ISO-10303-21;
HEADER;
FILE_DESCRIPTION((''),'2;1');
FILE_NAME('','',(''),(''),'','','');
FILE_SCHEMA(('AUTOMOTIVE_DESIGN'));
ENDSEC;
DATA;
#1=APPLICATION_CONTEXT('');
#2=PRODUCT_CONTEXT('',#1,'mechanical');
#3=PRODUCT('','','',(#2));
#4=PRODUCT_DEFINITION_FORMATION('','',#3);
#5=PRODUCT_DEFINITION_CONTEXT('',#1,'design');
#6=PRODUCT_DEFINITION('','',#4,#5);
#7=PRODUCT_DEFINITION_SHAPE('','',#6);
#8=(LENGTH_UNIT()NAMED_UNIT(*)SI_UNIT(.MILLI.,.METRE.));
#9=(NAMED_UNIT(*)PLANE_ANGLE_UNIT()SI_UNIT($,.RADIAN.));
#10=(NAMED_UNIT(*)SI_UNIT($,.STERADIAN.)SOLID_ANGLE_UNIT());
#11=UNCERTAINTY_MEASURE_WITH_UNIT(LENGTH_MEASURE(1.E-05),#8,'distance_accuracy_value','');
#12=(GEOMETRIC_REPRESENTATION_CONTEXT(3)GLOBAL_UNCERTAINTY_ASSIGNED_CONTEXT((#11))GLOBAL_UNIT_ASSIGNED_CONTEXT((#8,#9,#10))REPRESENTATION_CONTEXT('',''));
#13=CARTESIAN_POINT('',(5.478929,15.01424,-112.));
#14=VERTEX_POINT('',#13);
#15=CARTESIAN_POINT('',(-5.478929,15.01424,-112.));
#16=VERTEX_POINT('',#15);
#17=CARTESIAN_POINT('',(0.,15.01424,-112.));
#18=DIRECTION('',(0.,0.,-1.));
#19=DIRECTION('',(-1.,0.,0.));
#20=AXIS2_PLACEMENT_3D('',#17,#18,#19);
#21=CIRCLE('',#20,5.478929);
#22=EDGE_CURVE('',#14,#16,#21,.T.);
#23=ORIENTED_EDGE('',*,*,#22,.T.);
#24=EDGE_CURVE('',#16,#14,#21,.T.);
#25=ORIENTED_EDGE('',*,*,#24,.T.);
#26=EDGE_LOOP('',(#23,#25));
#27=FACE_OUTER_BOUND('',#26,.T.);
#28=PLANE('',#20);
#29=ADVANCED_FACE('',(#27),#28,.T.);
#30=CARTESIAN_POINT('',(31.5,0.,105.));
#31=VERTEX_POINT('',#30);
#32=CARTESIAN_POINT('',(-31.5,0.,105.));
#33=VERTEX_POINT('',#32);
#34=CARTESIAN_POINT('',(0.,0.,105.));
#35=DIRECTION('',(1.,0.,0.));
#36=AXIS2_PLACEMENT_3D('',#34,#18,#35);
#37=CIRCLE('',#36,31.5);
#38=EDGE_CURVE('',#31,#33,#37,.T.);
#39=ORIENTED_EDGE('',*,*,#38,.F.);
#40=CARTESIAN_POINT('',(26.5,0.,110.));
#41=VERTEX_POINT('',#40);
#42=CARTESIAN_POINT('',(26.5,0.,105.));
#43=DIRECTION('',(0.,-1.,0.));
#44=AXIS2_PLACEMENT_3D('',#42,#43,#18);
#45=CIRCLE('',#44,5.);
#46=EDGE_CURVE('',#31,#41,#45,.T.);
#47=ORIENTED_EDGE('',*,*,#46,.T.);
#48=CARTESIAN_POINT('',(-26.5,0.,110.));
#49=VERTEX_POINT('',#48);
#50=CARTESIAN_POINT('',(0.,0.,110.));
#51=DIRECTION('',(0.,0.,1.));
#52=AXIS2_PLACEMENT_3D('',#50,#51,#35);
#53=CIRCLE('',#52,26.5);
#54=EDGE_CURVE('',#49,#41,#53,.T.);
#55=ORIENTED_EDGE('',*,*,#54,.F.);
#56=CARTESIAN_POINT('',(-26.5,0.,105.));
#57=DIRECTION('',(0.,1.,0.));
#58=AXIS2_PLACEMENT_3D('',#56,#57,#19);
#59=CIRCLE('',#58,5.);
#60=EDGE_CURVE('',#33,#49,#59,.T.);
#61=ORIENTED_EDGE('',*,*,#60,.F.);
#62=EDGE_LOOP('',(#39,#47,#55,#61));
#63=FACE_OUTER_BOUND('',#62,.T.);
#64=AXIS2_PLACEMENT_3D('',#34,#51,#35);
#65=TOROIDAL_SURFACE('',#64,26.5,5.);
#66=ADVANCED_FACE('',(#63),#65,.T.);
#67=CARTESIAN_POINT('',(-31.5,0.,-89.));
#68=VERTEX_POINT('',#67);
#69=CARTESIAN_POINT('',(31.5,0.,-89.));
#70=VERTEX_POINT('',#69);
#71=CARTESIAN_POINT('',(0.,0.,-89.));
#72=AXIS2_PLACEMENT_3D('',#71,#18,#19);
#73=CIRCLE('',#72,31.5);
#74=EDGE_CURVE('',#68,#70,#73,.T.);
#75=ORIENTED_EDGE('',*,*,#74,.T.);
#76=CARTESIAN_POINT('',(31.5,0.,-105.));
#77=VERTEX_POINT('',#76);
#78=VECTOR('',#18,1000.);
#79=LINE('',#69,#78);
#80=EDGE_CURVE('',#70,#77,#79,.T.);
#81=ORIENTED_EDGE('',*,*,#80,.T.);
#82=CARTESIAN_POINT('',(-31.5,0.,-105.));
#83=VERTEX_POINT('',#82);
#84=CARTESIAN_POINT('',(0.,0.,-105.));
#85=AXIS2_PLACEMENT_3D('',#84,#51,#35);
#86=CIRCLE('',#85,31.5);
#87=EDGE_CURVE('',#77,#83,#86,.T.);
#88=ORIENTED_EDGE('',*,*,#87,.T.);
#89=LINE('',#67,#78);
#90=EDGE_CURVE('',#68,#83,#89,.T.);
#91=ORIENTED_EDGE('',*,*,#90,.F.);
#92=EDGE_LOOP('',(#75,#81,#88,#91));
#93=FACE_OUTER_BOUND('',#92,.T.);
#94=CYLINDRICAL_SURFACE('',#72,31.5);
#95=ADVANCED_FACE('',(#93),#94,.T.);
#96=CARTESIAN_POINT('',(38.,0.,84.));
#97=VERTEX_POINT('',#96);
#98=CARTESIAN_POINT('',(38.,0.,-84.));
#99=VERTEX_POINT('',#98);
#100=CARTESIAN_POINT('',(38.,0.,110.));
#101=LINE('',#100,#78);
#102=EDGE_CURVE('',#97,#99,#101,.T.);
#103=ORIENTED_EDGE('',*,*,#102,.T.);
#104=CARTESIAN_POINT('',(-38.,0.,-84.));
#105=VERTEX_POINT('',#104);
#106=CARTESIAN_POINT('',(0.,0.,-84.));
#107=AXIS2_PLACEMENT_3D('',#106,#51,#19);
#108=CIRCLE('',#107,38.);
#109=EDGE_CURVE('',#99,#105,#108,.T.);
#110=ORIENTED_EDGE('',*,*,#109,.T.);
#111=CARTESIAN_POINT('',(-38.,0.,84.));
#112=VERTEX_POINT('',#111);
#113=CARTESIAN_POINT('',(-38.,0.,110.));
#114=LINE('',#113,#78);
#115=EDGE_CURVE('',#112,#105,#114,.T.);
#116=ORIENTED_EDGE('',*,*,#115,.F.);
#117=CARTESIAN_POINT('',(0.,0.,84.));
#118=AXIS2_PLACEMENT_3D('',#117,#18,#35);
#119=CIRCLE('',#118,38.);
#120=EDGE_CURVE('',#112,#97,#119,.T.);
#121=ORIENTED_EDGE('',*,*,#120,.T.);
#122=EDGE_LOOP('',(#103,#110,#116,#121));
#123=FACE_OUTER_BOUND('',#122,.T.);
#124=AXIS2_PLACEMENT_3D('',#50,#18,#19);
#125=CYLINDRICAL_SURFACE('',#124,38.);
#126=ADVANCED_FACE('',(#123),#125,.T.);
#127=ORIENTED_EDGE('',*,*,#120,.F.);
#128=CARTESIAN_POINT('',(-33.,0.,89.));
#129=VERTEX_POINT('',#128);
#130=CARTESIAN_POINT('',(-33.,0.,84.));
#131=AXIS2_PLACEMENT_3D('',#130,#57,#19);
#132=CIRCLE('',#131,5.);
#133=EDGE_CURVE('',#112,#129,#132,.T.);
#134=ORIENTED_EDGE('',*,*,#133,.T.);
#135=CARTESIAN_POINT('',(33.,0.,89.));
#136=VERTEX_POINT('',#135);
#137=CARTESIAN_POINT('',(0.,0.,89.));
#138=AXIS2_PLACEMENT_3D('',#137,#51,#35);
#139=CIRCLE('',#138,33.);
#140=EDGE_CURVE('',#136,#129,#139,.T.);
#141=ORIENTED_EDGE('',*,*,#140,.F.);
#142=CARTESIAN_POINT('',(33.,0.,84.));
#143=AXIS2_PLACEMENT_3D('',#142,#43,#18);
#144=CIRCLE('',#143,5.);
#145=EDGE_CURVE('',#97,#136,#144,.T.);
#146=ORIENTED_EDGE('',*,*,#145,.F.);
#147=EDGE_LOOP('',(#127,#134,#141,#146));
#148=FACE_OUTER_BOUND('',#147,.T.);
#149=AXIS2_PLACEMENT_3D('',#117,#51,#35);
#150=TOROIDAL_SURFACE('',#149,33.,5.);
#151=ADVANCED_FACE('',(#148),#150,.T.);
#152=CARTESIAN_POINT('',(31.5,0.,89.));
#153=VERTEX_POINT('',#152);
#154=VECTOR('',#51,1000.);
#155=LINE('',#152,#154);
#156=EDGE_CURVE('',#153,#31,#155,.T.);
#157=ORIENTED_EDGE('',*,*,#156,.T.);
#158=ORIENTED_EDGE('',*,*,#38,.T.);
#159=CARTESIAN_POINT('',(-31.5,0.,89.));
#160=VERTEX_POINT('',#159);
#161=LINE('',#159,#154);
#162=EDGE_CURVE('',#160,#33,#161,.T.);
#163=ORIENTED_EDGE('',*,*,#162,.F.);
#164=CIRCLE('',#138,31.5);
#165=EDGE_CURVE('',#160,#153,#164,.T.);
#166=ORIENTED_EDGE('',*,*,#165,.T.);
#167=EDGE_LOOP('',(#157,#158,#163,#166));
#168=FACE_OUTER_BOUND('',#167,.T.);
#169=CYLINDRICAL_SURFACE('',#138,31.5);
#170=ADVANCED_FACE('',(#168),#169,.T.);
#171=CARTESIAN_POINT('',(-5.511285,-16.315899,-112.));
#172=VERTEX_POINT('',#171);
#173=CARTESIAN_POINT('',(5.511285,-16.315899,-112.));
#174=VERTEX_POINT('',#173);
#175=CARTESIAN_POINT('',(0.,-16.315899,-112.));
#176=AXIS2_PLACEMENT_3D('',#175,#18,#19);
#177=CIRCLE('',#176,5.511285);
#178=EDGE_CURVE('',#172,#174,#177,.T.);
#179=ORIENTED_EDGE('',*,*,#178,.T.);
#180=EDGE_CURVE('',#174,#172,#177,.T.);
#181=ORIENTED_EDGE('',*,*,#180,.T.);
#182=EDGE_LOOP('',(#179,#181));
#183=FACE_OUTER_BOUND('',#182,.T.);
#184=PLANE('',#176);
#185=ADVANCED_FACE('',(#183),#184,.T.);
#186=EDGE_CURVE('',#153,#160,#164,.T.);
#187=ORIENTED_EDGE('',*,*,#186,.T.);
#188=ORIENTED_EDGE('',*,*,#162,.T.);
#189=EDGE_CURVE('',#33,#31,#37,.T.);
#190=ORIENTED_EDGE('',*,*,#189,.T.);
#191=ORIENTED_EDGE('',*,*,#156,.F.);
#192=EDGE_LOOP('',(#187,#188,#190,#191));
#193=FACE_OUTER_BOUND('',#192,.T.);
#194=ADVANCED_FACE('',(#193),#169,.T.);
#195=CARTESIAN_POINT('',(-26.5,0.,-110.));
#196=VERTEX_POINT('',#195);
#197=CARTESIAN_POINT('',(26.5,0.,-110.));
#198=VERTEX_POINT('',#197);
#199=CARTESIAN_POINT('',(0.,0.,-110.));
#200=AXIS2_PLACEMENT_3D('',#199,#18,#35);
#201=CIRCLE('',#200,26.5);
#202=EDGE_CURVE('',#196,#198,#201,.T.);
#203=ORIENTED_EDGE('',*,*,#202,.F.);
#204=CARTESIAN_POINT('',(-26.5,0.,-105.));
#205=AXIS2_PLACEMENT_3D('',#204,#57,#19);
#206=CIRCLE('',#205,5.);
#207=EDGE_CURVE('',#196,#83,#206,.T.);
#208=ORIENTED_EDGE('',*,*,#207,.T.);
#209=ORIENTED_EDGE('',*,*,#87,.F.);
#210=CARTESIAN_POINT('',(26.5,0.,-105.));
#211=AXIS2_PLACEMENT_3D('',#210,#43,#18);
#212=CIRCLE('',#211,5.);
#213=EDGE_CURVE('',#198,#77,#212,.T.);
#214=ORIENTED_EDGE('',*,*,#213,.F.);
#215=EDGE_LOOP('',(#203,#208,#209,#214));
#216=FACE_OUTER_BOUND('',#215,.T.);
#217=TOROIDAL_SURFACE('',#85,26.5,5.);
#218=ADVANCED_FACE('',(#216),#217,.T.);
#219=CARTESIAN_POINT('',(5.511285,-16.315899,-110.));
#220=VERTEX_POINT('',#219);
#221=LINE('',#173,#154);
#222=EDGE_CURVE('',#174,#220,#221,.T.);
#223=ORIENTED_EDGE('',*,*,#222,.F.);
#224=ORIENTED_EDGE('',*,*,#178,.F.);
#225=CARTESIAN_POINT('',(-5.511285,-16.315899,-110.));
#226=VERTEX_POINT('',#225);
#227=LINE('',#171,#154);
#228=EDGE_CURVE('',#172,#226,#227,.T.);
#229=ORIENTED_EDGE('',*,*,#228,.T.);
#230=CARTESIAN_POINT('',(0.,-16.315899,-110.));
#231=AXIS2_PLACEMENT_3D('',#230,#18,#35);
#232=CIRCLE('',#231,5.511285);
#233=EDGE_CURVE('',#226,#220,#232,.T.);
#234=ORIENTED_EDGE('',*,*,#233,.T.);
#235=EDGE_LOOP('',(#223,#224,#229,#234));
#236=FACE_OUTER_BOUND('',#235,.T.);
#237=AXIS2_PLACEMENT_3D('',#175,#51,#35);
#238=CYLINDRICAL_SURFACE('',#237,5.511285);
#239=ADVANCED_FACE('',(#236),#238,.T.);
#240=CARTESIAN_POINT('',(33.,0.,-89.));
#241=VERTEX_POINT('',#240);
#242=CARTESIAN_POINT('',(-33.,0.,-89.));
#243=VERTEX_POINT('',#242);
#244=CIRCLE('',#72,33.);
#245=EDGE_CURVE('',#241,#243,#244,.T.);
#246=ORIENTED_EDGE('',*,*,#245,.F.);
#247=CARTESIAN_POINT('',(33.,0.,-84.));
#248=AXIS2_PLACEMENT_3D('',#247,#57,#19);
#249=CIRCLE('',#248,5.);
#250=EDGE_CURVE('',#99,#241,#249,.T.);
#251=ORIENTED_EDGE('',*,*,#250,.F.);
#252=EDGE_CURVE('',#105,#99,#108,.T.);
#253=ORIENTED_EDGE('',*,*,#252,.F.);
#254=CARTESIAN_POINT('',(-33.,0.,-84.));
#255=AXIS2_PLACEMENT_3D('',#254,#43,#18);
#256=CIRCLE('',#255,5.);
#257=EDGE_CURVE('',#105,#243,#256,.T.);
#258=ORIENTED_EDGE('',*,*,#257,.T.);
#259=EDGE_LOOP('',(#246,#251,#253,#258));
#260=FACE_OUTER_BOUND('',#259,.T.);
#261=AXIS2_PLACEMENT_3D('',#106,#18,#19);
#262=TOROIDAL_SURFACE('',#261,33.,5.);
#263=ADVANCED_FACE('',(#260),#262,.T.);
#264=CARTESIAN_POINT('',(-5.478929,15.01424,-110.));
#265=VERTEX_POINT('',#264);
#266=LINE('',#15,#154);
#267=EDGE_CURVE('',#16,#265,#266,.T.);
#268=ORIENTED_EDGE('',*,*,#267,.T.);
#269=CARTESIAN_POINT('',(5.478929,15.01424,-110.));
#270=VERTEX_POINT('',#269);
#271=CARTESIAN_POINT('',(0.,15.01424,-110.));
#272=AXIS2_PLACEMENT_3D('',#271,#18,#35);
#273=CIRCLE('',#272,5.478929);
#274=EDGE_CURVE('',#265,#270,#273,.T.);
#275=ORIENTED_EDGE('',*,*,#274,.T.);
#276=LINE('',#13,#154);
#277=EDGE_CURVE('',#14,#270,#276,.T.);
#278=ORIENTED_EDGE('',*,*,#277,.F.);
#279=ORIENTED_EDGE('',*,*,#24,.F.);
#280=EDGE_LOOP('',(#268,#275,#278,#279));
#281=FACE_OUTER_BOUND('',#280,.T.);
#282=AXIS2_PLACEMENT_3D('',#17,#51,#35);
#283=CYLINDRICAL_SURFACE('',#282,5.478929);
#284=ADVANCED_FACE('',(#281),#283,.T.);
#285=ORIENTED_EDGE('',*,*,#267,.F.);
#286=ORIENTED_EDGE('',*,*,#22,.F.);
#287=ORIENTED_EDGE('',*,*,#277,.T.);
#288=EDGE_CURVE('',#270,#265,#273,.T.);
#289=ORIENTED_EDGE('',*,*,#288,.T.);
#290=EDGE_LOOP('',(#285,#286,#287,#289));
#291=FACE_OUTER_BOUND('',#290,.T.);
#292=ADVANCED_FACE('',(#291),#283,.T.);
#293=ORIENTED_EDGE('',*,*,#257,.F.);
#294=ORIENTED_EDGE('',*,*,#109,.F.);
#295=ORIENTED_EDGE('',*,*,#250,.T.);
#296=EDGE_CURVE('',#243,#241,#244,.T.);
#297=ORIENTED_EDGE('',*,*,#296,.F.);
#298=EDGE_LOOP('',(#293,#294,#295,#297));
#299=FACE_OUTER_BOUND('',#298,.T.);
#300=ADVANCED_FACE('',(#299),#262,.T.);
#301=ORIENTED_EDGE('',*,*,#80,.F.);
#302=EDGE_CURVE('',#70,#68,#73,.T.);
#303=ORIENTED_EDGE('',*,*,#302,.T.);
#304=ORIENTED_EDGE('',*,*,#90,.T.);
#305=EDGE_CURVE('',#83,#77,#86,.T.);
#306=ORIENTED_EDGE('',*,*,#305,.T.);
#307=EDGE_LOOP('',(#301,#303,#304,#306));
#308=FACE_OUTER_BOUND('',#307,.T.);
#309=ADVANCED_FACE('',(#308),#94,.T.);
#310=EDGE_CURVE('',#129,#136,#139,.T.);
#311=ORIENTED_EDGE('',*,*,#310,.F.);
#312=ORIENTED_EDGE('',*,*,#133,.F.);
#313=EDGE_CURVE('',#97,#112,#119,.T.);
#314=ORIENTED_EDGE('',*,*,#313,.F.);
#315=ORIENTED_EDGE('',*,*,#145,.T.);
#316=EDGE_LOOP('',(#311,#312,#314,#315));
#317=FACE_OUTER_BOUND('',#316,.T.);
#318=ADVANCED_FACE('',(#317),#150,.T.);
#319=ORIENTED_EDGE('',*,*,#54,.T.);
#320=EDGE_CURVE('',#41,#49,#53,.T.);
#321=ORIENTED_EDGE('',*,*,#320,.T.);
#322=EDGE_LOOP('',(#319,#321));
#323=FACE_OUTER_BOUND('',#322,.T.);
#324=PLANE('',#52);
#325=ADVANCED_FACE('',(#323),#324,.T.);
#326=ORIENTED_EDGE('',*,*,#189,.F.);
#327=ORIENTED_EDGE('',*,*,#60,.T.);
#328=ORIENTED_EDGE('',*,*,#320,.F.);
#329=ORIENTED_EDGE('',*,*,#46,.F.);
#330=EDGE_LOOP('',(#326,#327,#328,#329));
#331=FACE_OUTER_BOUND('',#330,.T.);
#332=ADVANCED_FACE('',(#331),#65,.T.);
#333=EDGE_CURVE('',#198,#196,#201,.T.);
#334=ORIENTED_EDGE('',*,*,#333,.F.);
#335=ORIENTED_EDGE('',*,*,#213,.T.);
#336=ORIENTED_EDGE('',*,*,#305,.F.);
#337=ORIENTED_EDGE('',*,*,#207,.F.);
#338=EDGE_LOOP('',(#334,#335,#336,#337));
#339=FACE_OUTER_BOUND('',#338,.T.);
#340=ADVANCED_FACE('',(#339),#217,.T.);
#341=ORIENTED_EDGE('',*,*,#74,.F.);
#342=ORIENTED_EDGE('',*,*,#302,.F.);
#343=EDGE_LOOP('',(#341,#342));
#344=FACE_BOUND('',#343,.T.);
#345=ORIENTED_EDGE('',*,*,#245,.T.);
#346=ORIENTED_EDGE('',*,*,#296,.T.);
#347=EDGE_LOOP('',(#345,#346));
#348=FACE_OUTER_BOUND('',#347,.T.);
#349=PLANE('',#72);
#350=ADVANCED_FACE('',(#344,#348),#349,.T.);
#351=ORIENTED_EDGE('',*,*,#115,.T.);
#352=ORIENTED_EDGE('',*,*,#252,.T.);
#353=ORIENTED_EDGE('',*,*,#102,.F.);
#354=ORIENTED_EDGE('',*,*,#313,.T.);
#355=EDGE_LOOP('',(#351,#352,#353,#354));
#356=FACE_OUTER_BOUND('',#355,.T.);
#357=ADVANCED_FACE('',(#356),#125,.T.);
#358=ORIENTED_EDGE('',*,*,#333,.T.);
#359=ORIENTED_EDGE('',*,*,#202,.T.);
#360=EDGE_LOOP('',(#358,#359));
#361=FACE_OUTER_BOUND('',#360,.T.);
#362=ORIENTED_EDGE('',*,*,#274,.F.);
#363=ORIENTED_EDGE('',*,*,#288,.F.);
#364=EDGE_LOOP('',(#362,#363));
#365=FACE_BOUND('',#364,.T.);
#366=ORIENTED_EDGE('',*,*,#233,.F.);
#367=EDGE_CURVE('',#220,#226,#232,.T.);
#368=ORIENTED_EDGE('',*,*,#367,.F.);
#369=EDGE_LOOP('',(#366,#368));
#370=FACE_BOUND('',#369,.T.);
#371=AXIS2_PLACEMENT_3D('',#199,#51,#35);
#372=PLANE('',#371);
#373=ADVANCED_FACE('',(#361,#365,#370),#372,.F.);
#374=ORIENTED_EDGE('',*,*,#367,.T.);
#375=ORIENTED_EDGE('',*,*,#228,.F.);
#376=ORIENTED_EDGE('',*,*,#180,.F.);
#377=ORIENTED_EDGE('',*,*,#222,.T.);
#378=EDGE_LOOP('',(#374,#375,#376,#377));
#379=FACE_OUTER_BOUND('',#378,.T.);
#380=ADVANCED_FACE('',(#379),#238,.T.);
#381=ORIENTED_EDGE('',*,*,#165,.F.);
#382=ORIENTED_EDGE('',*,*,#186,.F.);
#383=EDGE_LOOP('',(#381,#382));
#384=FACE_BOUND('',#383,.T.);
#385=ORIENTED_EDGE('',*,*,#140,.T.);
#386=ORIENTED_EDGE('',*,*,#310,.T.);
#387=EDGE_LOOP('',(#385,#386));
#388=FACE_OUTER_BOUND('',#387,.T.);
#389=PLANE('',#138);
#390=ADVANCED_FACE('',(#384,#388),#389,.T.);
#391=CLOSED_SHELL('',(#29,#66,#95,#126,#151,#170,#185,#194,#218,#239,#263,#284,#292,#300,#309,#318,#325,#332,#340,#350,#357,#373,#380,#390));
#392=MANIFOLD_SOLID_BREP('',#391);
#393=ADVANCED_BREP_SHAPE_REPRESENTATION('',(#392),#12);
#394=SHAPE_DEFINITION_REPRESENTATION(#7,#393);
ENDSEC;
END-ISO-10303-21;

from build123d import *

# Parameters (mm, degrees)
SKETCH_1_R          = 38
EXTRUDE_1_DEPTH     = 110
SKETCH_4_OUTSIDE_W  = 126.97
SKETCH_4_OUTSIDE_H  = 126.97
SKETCH_4_OUTSIDE_R  = 31.5
CUT_EXTRUDE_1_DEPTH = 21
SKETCH_5_OUTSIDE_W  = 126.97
SKETCH_5_OUTSIDE_H  = 126.97
SKETCH_5_OUTSIDE_R  = 31.5
CUT_EXTRUDE_2_DEPTH = 21
FILLET_1_R          = 5
SKETCH_2_R          = 5.478928785
SKETCH_2_R_2        = 5.511284945
EXTRUDE_2_DEPTH     = 2


with BuildPart() as part:
    # 草图1 → 凸台-拉伸1 (new, symmetric)
    with BuildSketch(Plane.XY):
        Circle(SKETCH_1_R)
    extrude(amount=EXTRUDE_1_DEPTH, both=True)

    # 草图4 outside → 切除-拉伸1 (cut)
    with BuildSketch(Plane.XY.offset(110)):
        Rectangle(SKETCH_4_OUTSIDE_W, SKETCH_4_OUTSIDE_H)
        Circle(SKETCH_4_OUTSIDE_R, mode=Mode.SUBTRACT)
    extrude(amount=-CUT_EXTRUDE_1_DEPTH, mode=Mode.SUBTRACT)

    # 草图5 outside → 切除-拉伸2 (cut)
    with BuildSketch(Plane(origin=(0, 0, -110), x_dir=(-1, 0, 0), z_dir=(0, 0, -1))):
        Rectangle(SKETCH_5_OUTSIDE_W, SKETCH_5_OUTSIDE_H)
        with Locations(Location((0, 0, 0), (0, 0, 180))):
            Circle(SKETCH_5_OUTSIDE_R, mode=Mode.SUBTRACT)
    extrude(amount=-CUT_EXTRUDE_2_DEPTH, mode=Mode.SUBTRACT)

    # 圆角1
    fillet_1_edges = [part.edges().sort_by_distance(p)[0] for p in [
        (-31.5, 0, 110),
        (-38, 0, -89),
        (-31.5, 0, -110),
        (-38, 0, 89),
    ]]
    fillet(fillet_1_edges, radius=FILLET_1_R)

    # 草图2 → 凸台-拉伸2 (add)
    with BuildSketch(Plane(origin=(0, 0, -110), x_dir=(-1, 0, 0), z_dir=(0, 0, -1))):
        with Locations(Location((0, 15.014240139, 0), (0, 0, 180))):
            Circle(SKETCH_2_R)
        with Locations(Location((0, -16.315898799, 0), (0, 0, 180))):
            Circle(SKETCH_2_R_2)
    extrude(amount=EXTRUDE_2_DEPTH)


solid = part.part
